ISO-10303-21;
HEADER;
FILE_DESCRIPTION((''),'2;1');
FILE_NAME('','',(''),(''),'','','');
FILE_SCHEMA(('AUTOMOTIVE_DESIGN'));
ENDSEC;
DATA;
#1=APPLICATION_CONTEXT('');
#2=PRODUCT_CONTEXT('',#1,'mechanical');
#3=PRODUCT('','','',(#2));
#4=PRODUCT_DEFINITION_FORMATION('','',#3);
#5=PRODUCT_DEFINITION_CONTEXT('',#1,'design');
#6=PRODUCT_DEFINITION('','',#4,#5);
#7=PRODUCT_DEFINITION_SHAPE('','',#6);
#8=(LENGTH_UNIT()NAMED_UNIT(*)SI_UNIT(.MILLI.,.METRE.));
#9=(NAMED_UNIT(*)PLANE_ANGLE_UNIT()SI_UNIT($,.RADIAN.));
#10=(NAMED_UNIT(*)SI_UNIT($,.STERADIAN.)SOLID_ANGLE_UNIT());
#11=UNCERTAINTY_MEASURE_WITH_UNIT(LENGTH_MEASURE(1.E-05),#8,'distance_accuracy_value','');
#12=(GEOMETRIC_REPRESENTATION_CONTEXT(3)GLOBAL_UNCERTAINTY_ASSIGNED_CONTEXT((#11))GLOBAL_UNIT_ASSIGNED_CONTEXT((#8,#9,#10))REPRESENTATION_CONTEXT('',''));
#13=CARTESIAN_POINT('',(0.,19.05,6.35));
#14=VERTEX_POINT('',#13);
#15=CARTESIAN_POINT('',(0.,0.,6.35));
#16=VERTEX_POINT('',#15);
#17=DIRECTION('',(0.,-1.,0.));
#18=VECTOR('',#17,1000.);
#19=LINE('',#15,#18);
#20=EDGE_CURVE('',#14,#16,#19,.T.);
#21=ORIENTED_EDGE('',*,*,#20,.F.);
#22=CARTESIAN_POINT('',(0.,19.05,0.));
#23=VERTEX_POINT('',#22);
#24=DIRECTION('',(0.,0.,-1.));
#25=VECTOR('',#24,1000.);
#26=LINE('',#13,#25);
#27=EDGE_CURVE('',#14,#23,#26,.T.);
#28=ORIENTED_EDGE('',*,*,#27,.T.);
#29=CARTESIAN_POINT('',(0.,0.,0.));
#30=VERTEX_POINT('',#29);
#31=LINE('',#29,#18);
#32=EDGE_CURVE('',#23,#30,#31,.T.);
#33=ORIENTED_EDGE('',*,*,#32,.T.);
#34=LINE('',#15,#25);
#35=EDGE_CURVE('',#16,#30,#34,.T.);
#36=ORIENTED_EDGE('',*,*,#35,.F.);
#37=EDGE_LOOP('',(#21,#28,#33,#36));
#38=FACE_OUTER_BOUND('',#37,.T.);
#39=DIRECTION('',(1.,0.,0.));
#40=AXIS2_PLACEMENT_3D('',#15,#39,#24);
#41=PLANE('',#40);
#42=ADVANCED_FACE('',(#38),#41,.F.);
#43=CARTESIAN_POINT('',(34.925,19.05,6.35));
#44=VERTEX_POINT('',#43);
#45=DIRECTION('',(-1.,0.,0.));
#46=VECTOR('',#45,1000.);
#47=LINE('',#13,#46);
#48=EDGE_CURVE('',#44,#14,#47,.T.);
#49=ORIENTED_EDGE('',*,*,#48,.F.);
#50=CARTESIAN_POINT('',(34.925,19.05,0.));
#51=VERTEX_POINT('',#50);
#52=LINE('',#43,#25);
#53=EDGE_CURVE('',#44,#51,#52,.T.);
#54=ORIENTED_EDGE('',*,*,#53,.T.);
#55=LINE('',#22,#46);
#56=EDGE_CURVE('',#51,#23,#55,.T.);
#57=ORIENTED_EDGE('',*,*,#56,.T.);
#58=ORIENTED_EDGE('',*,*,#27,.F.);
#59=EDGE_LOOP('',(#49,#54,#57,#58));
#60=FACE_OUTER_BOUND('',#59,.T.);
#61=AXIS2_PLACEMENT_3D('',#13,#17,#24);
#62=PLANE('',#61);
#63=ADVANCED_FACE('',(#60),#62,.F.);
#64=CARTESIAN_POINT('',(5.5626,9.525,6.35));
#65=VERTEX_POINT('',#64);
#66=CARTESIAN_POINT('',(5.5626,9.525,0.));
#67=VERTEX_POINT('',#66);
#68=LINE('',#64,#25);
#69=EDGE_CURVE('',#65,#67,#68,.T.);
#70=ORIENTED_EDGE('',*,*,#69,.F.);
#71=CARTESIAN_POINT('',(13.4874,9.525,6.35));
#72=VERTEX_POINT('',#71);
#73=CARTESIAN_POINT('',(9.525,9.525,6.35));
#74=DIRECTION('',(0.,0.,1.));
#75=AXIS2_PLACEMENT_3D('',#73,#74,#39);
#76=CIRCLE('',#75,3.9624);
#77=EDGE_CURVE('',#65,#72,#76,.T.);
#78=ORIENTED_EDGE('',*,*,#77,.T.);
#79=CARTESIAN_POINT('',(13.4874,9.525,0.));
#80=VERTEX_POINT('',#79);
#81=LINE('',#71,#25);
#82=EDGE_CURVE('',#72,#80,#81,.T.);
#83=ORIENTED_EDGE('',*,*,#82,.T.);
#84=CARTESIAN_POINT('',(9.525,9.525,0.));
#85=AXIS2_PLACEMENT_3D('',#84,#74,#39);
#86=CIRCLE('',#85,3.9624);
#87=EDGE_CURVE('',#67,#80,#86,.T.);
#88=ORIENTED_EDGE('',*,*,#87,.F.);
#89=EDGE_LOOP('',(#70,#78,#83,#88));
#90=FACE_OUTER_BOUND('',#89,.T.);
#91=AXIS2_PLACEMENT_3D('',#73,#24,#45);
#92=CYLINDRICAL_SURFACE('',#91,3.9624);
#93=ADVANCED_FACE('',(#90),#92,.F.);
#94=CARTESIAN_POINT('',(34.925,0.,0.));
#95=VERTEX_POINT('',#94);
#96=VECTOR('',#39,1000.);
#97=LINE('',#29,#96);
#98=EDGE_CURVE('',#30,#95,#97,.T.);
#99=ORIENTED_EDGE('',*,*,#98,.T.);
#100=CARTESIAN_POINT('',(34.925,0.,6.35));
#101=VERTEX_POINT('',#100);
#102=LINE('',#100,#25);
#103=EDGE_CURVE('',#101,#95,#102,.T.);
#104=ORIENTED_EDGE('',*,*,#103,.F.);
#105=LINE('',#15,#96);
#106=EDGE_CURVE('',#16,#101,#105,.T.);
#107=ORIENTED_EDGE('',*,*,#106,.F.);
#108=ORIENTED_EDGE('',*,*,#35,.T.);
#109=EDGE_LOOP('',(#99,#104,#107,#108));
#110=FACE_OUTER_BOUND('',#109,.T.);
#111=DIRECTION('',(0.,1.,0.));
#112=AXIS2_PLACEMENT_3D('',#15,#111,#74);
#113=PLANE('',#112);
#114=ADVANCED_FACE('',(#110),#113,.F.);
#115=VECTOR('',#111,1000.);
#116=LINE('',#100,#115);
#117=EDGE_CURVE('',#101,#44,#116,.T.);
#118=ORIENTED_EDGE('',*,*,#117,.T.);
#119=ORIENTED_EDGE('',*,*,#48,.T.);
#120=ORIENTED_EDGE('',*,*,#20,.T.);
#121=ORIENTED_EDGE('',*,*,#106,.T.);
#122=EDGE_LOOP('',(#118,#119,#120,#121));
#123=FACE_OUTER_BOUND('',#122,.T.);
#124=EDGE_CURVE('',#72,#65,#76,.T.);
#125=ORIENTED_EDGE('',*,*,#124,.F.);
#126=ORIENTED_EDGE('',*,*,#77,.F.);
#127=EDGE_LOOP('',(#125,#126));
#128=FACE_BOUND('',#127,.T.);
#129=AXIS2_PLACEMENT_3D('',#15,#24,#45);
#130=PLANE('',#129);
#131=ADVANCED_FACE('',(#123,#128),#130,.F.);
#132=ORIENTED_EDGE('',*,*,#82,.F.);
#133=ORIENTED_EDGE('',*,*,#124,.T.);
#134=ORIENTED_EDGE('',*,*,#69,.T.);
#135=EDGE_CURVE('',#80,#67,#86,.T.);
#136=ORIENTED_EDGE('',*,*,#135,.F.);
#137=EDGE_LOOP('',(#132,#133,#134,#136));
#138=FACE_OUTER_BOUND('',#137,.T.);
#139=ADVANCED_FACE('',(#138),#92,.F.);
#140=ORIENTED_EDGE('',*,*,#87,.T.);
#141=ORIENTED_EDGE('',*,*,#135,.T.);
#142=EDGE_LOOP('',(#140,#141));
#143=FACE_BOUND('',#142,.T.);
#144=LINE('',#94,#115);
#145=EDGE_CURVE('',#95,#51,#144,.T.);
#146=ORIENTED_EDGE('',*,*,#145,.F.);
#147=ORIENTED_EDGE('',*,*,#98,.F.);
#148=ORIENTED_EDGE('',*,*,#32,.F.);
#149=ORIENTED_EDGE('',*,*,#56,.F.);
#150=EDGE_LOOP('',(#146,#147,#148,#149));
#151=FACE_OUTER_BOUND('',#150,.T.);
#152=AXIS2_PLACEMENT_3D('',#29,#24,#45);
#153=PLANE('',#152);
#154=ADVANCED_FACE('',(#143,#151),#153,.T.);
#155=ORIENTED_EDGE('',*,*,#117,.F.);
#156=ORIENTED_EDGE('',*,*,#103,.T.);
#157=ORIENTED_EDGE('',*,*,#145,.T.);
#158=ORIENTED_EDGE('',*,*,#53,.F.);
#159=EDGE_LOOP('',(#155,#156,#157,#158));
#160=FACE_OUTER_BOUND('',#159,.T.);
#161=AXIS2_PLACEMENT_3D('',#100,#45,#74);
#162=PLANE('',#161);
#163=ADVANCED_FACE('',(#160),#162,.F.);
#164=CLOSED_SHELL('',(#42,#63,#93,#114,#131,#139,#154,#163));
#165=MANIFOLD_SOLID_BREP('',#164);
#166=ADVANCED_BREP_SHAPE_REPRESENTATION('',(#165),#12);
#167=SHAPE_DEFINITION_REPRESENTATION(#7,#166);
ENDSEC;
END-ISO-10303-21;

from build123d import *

# Parameters (mm, degrees)
SKETCH1_W           = 34.925
SKETCH1_H           = 19.05
SKETCH1_R           = 3.9624
BOSS_EXTRUDE1_DEPTH = 6.35


with BuildPart() as part:
    # Sketch1 → Boss-Extrude1 (new body)
    with BuildSketch(Plane.XY):
        with Locations((17.4625, 9.525)):
            Rectangle(SKETCH1_W, SKETCH1_H)
        with Locations((9.525, 9.525)):
            Circle(SKETCH1_R, mode=Mode.SUBTRACT)
    extrude(amount=BOSS_EXTRUDE1_DEPTH)


solid = part.part
